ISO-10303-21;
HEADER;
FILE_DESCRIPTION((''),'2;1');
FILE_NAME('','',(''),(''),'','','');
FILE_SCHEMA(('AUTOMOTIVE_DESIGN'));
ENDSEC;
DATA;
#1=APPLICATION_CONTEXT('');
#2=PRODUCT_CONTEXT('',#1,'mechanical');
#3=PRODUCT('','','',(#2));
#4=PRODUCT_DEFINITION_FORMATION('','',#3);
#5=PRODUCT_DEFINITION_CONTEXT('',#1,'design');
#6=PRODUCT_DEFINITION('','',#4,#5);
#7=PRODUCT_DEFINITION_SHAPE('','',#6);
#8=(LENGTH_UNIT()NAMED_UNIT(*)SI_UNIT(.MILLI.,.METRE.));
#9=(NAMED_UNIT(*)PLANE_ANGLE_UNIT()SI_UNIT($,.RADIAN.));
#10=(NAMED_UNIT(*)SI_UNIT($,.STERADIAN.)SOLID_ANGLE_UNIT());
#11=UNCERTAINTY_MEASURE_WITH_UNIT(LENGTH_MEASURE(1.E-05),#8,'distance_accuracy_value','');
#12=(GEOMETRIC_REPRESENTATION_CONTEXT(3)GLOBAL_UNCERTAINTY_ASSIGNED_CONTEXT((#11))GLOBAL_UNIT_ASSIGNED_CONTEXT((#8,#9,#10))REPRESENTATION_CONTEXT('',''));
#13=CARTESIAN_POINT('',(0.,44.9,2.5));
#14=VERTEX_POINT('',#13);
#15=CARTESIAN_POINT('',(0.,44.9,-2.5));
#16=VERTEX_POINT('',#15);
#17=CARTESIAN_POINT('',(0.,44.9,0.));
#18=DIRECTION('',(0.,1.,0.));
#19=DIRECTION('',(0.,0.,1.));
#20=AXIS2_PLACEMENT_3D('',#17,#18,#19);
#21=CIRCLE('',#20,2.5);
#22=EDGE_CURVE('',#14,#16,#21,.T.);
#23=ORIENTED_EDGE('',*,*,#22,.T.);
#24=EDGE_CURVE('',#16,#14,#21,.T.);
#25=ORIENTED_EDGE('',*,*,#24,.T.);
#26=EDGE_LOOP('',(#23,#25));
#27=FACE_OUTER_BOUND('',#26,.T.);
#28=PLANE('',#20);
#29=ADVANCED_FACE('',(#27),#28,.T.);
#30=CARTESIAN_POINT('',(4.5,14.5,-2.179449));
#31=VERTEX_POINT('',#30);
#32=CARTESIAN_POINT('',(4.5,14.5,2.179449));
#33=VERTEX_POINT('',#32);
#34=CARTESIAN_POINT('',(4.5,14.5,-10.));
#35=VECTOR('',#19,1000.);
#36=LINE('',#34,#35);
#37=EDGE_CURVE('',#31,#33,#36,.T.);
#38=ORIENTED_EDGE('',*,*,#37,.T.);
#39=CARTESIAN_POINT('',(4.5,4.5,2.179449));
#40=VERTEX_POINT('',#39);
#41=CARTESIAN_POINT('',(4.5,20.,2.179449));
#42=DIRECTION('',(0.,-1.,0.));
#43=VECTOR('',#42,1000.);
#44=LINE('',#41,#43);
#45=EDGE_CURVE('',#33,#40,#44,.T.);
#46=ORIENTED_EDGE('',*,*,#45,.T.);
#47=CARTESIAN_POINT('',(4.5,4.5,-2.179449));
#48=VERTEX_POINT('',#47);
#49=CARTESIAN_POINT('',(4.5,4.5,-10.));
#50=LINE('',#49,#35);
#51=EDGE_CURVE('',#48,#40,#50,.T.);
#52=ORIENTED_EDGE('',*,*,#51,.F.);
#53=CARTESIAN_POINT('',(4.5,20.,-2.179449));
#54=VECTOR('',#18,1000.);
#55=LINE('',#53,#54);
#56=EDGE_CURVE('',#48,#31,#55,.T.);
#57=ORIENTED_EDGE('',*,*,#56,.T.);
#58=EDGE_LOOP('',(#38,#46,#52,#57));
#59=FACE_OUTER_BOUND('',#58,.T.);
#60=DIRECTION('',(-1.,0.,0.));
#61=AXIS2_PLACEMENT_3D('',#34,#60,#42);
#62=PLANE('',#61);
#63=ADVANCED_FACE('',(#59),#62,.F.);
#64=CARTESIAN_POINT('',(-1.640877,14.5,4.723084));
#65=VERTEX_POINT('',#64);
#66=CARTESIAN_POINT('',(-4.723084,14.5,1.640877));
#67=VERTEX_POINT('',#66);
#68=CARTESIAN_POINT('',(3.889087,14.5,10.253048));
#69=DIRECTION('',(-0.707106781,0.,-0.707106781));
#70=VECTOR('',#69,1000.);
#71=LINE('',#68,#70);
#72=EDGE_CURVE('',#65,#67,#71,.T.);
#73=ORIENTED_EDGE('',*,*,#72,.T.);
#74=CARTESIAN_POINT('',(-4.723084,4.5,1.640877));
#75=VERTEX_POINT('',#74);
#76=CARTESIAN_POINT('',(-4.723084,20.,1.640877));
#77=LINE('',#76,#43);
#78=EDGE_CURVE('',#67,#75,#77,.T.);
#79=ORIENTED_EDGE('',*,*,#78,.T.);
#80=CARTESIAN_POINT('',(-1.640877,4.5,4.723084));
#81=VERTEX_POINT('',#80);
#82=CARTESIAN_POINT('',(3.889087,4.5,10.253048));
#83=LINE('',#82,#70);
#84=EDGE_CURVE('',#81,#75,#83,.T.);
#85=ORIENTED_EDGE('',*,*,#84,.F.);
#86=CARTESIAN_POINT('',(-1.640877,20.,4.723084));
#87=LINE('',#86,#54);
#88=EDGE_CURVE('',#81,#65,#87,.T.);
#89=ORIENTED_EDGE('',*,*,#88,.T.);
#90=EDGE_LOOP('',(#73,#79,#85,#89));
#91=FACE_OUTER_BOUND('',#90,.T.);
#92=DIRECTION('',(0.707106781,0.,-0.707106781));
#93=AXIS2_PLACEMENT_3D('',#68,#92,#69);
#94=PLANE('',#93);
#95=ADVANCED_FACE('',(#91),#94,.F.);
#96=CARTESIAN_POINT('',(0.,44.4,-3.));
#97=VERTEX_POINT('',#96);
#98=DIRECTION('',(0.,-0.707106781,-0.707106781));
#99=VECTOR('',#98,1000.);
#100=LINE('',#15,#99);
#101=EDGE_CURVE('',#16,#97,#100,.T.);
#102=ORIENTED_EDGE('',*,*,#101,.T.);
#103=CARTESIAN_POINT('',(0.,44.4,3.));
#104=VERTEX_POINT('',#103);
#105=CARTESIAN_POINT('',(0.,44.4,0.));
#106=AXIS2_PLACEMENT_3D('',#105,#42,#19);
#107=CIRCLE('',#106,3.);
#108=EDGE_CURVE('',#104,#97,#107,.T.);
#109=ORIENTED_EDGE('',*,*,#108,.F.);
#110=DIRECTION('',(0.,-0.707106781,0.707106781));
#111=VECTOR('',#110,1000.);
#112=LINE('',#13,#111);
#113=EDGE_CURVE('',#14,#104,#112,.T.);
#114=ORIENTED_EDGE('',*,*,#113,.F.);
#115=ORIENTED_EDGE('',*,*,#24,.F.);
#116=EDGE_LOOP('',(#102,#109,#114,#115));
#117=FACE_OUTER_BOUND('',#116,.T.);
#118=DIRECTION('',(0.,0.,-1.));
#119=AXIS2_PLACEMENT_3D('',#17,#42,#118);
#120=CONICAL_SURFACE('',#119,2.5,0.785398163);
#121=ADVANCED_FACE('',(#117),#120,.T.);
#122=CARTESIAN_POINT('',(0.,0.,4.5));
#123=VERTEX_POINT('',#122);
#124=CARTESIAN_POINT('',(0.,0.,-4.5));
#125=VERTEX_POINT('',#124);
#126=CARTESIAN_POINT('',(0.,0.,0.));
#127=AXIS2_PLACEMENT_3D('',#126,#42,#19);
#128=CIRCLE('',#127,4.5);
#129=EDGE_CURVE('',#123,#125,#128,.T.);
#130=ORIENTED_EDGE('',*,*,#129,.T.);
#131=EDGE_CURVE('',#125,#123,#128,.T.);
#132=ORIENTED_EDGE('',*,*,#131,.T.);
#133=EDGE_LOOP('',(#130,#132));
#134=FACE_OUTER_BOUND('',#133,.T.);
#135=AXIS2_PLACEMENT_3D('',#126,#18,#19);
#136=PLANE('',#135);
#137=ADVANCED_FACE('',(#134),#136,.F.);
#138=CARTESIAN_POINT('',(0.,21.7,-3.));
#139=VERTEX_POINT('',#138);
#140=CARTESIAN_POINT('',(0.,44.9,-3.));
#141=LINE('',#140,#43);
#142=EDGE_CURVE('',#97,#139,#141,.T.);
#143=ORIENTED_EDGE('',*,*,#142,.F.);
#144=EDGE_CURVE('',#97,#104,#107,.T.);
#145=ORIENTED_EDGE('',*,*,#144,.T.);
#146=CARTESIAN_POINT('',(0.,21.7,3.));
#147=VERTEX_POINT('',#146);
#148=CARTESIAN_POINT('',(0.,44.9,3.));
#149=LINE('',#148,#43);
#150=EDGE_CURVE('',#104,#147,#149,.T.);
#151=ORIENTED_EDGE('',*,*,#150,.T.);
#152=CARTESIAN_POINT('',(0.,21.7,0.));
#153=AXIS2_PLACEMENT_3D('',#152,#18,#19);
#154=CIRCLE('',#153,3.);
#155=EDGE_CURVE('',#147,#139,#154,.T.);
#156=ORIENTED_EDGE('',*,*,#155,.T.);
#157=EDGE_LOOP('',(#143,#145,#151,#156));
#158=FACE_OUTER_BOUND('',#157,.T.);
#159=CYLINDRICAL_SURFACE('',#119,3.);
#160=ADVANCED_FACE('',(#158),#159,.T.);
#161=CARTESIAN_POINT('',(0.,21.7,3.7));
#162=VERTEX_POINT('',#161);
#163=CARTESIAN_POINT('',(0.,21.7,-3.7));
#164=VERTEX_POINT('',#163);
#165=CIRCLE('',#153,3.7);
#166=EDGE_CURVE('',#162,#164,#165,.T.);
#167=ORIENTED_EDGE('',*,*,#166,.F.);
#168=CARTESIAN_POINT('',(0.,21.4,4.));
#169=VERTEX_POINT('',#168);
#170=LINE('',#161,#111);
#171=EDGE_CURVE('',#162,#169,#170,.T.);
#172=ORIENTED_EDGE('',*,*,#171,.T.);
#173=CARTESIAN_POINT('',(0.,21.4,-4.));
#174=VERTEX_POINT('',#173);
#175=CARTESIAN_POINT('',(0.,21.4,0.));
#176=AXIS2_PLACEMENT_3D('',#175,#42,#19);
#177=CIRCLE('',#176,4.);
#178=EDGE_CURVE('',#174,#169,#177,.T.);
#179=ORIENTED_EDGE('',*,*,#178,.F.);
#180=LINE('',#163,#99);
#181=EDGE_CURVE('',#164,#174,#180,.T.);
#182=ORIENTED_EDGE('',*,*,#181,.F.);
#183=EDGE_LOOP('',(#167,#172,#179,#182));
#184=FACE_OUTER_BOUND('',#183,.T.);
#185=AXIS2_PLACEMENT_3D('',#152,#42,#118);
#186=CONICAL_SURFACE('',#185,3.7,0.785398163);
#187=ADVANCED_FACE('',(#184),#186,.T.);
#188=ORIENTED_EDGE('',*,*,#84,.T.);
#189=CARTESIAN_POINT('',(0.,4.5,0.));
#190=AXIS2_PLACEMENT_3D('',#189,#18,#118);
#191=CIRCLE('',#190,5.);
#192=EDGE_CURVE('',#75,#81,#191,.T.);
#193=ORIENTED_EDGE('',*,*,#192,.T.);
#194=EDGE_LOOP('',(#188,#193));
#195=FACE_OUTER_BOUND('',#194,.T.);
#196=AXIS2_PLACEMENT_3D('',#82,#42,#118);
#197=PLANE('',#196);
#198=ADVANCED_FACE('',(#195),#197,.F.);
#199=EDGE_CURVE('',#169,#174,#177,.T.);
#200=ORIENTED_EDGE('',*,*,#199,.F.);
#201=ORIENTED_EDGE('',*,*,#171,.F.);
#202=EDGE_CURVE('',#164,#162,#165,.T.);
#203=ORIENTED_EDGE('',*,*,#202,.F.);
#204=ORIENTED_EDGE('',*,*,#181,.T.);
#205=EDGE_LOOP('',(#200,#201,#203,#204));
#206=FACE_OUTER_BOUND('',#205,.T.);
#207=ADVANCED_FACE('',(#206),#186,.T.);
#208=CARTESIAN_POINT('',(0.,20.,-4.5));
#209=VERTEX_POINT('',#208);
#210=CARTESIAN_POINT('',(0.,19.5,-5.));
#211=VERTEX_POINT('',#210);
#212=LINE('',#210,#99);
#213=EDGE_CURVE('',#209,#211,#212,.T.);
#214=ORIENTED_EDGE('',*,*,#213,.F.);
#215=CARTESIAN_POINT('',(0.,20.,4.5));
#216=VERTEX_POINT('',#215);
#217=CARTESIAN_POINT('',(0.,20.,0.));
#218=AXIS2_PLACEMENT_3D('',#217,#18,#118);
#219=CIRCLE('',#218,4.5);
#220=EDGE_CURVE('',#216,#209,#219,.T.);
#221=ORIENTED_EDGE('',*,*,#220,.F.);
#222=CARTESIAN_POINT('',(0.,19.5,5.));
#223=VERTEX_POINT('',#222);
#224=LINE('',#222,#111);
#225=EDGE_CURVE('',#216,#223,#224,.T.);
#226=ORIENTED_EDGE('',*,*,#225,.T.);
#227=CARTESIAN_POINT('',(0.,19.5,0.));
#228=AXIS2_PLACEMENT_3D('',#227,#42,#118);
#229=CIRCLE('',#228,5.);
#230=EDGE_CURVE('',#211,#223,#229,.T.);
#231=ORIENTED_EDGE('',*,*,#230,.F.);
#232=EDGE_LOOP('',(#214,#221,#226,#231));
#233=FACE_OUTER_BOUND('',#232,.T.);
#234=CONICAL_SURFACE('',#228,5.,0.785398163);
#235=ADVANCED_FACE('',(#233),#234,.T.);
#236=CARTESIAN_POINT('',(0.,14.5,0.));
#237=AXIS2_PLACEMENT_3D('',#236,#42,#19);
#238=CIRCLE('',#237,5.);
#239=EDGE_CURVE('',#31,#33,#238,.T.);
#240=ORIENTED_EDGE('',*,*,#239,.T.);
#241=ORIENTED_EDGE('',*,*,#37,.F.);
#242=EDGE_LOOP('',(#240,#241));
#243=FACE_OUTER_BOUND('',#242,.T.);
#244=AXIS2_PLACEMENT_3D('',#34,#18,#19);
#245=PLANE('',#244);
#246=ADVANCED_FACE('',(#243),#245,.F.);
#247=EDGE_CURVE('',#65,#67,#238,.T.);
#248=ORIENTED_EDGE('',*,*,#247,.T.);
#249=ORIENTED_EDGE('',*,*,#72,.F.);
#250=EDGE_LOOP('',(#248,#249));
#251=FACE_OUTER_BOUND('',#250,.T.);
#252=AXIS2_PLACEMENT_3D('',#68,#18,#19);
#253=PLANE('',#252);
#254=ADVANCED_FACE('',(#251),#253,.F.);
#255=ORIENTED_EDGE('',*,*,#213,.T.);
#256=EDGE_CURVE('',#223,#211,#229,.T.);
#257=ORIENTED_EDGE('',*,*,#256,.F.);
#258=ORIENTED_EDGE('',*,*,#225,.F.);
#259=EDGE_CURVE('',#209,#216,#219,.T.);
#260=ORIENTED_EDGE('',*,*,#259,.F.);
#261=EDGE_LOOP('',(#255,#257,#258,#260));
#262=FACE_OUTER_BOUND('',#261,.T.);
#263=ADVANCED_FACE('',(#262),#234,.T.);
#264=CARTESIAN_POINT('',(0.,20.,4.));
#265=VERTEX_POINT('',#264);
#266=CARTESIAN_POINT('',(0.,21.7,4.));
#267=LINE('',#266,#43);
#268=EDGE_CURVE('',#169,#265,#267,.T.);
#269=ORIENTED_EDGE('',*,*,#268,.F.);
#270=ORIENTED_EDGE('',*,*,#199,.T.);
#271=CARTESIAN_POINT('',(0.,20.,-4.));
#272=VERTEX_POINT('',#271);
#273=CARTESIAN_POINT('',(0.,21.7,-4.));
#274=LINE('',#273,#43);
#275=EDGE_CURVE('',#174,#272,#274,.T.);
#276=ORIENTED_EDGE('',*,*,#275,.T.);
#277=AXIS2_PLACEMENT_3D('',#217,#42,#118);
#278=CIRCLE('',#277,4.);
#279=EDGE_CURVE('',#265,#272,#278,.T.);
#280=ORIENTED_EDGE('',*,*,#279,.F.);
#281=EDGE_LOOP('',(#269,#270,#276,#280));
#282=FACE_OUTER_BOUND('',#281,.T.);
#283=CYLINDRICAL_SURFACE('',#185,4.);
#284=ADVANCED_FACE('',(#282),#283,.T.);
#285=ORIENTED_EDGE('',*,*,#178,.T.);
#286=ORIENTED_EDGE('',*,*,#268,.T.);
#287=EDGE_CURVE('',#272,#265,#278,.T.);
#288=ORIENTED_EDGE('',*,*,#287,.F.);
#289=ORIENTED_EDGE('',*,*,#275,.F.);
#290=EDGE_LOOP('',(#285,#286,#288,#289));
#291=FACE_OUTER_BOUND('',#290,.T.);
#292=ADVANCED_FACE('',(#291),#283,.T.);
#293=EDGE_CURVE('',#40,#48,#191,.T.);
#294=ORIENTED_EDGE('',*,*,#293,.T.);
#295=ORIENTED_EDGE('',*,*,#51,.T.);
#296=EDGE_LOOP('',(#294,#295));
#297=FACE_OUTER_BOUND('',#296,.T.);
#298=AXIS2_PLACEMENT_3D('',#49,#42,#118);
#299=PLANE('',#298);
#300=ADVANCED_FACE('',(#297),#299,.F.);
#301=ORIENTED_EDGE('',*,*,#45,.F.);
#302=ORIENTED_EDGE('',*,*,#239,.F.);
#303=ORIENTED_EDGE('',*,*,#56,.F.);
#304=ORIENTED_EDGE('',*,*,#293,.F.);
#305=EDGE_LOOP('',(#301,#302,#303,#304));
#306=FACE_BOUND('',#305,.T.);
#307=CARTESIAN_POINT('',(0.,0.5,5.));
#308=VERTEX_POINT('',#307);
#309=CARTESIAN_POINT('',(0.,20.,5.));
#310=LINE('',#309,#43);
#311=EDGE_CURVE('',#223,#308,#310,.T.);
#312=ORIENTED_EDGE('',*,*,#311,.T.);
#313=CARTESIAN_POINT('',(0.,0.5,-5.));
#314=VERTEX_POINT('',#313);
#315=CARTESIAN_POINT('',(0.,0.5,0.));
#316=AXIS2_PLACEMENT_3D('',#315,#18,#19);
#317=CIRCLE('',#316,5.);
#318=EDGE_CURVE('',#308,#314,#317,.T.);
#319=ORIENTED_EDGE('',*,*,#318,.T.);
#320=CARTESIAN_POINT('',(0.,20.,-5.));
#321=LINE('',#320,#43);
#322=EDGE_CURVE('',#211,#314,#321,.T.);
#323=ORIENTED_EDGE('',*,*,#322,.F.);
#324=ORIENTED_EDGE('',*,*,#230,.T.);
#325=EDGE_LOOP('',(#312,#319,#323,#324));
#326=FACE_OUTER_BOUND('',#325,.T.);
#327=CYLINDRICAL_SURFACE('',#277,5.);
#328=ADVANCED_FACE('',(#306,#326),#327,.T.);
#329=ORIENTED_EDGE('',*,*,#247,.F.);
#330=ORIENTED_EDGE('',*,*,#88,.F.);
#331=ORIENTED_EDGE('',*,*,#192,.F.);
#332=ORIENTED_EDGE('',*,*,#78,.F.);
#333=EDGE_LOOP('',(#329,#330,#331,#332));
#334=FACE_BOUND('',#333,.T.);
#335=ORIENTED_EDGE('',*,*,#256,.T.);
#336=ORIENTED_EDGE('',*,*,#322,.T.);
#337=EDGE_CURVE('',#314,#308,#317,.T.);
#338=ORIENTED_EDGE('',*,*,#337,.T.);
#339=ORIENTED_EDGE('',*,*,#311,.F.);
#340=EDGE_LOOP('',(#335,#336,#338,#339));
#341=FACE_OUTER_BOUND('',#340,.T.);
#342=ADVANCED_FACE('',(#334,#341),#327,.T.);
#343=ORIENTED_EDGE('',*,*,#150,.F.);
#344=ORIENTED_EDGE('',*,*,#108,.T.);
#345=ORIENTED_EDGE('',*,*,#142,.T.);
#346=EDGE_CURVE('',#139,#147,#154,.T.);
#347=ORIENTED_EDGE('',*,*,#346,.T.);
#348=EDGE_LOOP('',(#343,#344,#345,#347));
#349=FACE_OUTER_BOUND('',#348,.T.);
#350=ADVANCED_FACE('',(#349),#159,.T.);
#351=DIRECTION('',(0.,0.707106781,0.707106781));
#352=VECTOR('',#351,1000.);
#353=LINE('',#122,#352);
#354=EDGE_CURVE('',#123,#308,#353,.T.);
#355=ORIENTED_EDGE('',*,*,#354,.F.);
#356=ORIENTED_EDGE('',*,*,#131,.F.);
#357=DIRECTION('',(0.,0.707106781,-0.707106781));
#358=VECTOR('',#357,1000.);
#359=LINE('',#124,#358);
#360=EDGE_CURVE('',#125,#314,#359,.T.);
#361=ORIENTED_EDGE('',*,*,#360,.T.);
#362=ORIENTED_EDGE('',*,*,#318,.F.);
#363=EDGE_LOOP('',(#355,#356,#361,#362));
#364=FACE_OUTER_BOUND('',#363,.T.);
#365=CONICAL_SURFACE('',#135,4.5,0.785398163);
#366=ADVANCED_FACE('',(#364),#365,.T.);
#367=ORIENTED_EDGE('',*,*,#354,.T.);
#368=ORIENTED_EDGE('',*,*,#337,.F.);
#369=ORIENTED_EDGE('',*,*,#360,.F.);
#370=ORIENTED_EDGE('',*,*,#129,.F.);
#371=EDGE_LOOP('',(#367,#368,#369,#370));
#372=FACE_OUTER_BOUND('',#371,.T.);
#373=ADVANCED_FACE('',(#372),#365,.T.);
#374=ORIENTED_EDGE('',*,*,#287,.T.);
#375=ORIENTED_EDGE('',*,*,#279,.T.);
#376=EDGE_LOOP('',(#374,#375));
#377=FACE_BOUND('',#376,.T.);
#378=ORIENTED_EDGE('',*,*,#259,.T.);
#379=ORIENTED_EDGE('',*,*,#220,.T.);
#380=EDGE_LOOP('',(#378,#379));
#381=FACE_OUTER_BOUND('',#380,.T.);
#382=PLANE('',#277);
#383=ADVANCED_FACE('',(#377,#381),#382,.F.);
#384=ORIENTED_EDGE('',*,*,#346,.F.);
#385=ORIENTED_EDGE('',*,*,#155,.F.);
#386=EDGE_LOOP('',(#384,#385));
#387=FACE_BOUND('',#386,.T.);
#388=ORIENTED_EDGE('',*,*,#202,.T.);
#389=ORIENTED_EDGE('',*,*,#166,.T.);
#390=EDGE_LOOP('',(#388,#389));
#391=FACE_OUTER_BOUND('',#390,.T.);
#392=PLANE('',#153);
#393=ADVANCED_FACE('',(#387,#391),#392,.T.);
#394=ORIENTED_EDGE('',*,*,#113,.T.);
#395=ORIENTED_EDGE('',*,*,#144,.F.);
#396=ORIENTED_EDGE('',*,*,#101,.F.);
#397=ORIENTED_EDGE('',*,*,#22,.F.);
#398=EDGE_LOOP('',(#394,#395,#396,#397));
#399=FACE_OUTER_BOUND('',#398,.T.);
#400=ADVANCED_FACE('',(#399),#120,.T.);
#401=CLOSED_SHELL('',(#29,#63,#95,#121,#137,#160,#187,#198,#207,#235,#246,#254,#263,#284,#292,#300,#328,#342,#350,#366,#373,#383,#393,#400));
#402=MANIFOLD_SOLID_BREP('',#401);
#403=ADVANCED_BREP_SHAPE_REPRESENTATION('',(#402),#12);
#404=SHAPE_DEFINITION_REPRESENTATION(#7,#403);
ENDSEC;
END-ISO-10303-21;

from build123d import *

# Parameters (mm, degrees)
SKETCH1_R           = 3
BOSS_EXTRUDE1_DEPTH = 20.5
SKETCH2_R           = 4
BOSS_EXTRUDE2_DEPTH = 1.2
SKETCH5_R           = 3
BOSS_EXTRUDE3_DEPTH = 23.2
CHAMFER3_SIZE       = 0.5
BOSS_EXTRUDE4_START = 20.5
SKETCH6_R           = 4
BOSS_EXTRUDE4_DEPTH = 20.5
CHAMFER4_SIZE       = 0.3
SKETCH9_R           = 5
BOSS_EXTRUDE5_DEPTH = 20
CHAMFER5_SIZE       = 0.5
SKETCH10_W          = 1
SKETCH10_H          = 10
CUT_EXTRUDE2_DEPTH  = 10
CIRPATTERN2_COUNT   = 2
CIRPATTERN2_ANGLE   = 135


with BuildPart() as part:
    # Sketch1 → Boss-Extrude1 (new body)
    with BuildSketch(Plane(origin=(0, 0, 0), x_dir=(1, 0, 0), z_dir=(0, 1, 0))):
        with Locations(Location((0, 0, 0), (0, 0, 270))):
            Circle(SKETCH1_R)
    extrude(amount=BOSS_EXTRUDE1_DEPTH)

    # Sketch2 → Boss-Extrude2 (add)
    with BuildSketch(Plane(origin=(0, 20.5, 0), x_dir=(1, 0, 0), z_dir=(0, 1, 0))):
        with Locations(Location((0, 0, 0), (0, 0, 270))):
            Circle(SKETCH2_R)
    extrude(amount=BOSS_EXTRUDE2_DEPTH)

    # Sketch5 → Boss-Extrude3 (add)
    with BuildSketch(Plane(origin=(0, 21.7, 0), x_dir=(1, 0, 0), z_dir=(0, 1, 0))):
        with Locations(Location((0, 0, 0), (0, 0, 270))):
            Circle(SKETCH5_R)
    extrude(amount=BOSS_EXTRUDE3_DEPTH)

    # Chamfer3
    chamfer3_edges = [part.edges().sort_by_distance(p)[0] for p in [
        (0, 44.9, -3),
    ]]
    chamfer(chamfer3_edges, length=CHAMFER3_SIZE)

    # Sketch6 → Boss-Extrude4 (add)
    with BuildSketch(Plane.XZ.offset(-20.5).offset(BOSS_EXTRUDE4_START)):
        with Locations(Location((0, 0, 0), (0, 0, 90))):
            Circle(SKETCH6_R)
    extrude(amount=-BOSS_EXTRUDE4_DEPTH)

    # Chamfer4
    chamfer4_edges = [part.edges().sort_by_distance(p)[0] for p in [
        (0, 21.7, -4),
    ]]
    chamfer(chamfer4_edges, length=CHAMFER4_SIZE)

    # Sketch9 → Boss-Extrude5 (add)
    with BuildSketch(Plane.XZ):
        with Locations(Location((0, 0, 0), (0, 0, 270))):
            Circle(SKETCH9_R)
    extrude(amount=-BOSS_EXTRUDE5_DEPTH)

    # Chamfer5
    chamfer5_edges = [part.edges().sort_by_distance(p)[0] for p in [
        (0, 0, 5),
        (0, 20, 5),
    ]]
    chamfer(chamfer5_edges, length=CHAMFER5_SIZE)

    # Sketch10 → Cut-Extrude2 (cut, symmetric)
    with BuildSketch(Plane.XY):
        with Locations((5, 9.5)):
            Rectangle(SKETCH10_W, SKETCH10_H)
    cut_extrude2 = extrude(amount=CUT_EXTRUDE2_DEPTH, both=True, mode=Mode.SUBTRACT)

    # CirPattern2: Cut-Extrude2 ×2 about axis
    cirpattern2_axis = Axis((0, 44.9, 0), (0, -1, 0))
    for i in range(1, CIRPATTERN2_COUNT):
        add(cut_extrude2.rotate(cirpattern2_axis, i * CIRPATTERN2_ANGLE / (CIRPATTERN2_COUNT - 1)), mode=Mode.SUBTRACT)


solid = part.part
